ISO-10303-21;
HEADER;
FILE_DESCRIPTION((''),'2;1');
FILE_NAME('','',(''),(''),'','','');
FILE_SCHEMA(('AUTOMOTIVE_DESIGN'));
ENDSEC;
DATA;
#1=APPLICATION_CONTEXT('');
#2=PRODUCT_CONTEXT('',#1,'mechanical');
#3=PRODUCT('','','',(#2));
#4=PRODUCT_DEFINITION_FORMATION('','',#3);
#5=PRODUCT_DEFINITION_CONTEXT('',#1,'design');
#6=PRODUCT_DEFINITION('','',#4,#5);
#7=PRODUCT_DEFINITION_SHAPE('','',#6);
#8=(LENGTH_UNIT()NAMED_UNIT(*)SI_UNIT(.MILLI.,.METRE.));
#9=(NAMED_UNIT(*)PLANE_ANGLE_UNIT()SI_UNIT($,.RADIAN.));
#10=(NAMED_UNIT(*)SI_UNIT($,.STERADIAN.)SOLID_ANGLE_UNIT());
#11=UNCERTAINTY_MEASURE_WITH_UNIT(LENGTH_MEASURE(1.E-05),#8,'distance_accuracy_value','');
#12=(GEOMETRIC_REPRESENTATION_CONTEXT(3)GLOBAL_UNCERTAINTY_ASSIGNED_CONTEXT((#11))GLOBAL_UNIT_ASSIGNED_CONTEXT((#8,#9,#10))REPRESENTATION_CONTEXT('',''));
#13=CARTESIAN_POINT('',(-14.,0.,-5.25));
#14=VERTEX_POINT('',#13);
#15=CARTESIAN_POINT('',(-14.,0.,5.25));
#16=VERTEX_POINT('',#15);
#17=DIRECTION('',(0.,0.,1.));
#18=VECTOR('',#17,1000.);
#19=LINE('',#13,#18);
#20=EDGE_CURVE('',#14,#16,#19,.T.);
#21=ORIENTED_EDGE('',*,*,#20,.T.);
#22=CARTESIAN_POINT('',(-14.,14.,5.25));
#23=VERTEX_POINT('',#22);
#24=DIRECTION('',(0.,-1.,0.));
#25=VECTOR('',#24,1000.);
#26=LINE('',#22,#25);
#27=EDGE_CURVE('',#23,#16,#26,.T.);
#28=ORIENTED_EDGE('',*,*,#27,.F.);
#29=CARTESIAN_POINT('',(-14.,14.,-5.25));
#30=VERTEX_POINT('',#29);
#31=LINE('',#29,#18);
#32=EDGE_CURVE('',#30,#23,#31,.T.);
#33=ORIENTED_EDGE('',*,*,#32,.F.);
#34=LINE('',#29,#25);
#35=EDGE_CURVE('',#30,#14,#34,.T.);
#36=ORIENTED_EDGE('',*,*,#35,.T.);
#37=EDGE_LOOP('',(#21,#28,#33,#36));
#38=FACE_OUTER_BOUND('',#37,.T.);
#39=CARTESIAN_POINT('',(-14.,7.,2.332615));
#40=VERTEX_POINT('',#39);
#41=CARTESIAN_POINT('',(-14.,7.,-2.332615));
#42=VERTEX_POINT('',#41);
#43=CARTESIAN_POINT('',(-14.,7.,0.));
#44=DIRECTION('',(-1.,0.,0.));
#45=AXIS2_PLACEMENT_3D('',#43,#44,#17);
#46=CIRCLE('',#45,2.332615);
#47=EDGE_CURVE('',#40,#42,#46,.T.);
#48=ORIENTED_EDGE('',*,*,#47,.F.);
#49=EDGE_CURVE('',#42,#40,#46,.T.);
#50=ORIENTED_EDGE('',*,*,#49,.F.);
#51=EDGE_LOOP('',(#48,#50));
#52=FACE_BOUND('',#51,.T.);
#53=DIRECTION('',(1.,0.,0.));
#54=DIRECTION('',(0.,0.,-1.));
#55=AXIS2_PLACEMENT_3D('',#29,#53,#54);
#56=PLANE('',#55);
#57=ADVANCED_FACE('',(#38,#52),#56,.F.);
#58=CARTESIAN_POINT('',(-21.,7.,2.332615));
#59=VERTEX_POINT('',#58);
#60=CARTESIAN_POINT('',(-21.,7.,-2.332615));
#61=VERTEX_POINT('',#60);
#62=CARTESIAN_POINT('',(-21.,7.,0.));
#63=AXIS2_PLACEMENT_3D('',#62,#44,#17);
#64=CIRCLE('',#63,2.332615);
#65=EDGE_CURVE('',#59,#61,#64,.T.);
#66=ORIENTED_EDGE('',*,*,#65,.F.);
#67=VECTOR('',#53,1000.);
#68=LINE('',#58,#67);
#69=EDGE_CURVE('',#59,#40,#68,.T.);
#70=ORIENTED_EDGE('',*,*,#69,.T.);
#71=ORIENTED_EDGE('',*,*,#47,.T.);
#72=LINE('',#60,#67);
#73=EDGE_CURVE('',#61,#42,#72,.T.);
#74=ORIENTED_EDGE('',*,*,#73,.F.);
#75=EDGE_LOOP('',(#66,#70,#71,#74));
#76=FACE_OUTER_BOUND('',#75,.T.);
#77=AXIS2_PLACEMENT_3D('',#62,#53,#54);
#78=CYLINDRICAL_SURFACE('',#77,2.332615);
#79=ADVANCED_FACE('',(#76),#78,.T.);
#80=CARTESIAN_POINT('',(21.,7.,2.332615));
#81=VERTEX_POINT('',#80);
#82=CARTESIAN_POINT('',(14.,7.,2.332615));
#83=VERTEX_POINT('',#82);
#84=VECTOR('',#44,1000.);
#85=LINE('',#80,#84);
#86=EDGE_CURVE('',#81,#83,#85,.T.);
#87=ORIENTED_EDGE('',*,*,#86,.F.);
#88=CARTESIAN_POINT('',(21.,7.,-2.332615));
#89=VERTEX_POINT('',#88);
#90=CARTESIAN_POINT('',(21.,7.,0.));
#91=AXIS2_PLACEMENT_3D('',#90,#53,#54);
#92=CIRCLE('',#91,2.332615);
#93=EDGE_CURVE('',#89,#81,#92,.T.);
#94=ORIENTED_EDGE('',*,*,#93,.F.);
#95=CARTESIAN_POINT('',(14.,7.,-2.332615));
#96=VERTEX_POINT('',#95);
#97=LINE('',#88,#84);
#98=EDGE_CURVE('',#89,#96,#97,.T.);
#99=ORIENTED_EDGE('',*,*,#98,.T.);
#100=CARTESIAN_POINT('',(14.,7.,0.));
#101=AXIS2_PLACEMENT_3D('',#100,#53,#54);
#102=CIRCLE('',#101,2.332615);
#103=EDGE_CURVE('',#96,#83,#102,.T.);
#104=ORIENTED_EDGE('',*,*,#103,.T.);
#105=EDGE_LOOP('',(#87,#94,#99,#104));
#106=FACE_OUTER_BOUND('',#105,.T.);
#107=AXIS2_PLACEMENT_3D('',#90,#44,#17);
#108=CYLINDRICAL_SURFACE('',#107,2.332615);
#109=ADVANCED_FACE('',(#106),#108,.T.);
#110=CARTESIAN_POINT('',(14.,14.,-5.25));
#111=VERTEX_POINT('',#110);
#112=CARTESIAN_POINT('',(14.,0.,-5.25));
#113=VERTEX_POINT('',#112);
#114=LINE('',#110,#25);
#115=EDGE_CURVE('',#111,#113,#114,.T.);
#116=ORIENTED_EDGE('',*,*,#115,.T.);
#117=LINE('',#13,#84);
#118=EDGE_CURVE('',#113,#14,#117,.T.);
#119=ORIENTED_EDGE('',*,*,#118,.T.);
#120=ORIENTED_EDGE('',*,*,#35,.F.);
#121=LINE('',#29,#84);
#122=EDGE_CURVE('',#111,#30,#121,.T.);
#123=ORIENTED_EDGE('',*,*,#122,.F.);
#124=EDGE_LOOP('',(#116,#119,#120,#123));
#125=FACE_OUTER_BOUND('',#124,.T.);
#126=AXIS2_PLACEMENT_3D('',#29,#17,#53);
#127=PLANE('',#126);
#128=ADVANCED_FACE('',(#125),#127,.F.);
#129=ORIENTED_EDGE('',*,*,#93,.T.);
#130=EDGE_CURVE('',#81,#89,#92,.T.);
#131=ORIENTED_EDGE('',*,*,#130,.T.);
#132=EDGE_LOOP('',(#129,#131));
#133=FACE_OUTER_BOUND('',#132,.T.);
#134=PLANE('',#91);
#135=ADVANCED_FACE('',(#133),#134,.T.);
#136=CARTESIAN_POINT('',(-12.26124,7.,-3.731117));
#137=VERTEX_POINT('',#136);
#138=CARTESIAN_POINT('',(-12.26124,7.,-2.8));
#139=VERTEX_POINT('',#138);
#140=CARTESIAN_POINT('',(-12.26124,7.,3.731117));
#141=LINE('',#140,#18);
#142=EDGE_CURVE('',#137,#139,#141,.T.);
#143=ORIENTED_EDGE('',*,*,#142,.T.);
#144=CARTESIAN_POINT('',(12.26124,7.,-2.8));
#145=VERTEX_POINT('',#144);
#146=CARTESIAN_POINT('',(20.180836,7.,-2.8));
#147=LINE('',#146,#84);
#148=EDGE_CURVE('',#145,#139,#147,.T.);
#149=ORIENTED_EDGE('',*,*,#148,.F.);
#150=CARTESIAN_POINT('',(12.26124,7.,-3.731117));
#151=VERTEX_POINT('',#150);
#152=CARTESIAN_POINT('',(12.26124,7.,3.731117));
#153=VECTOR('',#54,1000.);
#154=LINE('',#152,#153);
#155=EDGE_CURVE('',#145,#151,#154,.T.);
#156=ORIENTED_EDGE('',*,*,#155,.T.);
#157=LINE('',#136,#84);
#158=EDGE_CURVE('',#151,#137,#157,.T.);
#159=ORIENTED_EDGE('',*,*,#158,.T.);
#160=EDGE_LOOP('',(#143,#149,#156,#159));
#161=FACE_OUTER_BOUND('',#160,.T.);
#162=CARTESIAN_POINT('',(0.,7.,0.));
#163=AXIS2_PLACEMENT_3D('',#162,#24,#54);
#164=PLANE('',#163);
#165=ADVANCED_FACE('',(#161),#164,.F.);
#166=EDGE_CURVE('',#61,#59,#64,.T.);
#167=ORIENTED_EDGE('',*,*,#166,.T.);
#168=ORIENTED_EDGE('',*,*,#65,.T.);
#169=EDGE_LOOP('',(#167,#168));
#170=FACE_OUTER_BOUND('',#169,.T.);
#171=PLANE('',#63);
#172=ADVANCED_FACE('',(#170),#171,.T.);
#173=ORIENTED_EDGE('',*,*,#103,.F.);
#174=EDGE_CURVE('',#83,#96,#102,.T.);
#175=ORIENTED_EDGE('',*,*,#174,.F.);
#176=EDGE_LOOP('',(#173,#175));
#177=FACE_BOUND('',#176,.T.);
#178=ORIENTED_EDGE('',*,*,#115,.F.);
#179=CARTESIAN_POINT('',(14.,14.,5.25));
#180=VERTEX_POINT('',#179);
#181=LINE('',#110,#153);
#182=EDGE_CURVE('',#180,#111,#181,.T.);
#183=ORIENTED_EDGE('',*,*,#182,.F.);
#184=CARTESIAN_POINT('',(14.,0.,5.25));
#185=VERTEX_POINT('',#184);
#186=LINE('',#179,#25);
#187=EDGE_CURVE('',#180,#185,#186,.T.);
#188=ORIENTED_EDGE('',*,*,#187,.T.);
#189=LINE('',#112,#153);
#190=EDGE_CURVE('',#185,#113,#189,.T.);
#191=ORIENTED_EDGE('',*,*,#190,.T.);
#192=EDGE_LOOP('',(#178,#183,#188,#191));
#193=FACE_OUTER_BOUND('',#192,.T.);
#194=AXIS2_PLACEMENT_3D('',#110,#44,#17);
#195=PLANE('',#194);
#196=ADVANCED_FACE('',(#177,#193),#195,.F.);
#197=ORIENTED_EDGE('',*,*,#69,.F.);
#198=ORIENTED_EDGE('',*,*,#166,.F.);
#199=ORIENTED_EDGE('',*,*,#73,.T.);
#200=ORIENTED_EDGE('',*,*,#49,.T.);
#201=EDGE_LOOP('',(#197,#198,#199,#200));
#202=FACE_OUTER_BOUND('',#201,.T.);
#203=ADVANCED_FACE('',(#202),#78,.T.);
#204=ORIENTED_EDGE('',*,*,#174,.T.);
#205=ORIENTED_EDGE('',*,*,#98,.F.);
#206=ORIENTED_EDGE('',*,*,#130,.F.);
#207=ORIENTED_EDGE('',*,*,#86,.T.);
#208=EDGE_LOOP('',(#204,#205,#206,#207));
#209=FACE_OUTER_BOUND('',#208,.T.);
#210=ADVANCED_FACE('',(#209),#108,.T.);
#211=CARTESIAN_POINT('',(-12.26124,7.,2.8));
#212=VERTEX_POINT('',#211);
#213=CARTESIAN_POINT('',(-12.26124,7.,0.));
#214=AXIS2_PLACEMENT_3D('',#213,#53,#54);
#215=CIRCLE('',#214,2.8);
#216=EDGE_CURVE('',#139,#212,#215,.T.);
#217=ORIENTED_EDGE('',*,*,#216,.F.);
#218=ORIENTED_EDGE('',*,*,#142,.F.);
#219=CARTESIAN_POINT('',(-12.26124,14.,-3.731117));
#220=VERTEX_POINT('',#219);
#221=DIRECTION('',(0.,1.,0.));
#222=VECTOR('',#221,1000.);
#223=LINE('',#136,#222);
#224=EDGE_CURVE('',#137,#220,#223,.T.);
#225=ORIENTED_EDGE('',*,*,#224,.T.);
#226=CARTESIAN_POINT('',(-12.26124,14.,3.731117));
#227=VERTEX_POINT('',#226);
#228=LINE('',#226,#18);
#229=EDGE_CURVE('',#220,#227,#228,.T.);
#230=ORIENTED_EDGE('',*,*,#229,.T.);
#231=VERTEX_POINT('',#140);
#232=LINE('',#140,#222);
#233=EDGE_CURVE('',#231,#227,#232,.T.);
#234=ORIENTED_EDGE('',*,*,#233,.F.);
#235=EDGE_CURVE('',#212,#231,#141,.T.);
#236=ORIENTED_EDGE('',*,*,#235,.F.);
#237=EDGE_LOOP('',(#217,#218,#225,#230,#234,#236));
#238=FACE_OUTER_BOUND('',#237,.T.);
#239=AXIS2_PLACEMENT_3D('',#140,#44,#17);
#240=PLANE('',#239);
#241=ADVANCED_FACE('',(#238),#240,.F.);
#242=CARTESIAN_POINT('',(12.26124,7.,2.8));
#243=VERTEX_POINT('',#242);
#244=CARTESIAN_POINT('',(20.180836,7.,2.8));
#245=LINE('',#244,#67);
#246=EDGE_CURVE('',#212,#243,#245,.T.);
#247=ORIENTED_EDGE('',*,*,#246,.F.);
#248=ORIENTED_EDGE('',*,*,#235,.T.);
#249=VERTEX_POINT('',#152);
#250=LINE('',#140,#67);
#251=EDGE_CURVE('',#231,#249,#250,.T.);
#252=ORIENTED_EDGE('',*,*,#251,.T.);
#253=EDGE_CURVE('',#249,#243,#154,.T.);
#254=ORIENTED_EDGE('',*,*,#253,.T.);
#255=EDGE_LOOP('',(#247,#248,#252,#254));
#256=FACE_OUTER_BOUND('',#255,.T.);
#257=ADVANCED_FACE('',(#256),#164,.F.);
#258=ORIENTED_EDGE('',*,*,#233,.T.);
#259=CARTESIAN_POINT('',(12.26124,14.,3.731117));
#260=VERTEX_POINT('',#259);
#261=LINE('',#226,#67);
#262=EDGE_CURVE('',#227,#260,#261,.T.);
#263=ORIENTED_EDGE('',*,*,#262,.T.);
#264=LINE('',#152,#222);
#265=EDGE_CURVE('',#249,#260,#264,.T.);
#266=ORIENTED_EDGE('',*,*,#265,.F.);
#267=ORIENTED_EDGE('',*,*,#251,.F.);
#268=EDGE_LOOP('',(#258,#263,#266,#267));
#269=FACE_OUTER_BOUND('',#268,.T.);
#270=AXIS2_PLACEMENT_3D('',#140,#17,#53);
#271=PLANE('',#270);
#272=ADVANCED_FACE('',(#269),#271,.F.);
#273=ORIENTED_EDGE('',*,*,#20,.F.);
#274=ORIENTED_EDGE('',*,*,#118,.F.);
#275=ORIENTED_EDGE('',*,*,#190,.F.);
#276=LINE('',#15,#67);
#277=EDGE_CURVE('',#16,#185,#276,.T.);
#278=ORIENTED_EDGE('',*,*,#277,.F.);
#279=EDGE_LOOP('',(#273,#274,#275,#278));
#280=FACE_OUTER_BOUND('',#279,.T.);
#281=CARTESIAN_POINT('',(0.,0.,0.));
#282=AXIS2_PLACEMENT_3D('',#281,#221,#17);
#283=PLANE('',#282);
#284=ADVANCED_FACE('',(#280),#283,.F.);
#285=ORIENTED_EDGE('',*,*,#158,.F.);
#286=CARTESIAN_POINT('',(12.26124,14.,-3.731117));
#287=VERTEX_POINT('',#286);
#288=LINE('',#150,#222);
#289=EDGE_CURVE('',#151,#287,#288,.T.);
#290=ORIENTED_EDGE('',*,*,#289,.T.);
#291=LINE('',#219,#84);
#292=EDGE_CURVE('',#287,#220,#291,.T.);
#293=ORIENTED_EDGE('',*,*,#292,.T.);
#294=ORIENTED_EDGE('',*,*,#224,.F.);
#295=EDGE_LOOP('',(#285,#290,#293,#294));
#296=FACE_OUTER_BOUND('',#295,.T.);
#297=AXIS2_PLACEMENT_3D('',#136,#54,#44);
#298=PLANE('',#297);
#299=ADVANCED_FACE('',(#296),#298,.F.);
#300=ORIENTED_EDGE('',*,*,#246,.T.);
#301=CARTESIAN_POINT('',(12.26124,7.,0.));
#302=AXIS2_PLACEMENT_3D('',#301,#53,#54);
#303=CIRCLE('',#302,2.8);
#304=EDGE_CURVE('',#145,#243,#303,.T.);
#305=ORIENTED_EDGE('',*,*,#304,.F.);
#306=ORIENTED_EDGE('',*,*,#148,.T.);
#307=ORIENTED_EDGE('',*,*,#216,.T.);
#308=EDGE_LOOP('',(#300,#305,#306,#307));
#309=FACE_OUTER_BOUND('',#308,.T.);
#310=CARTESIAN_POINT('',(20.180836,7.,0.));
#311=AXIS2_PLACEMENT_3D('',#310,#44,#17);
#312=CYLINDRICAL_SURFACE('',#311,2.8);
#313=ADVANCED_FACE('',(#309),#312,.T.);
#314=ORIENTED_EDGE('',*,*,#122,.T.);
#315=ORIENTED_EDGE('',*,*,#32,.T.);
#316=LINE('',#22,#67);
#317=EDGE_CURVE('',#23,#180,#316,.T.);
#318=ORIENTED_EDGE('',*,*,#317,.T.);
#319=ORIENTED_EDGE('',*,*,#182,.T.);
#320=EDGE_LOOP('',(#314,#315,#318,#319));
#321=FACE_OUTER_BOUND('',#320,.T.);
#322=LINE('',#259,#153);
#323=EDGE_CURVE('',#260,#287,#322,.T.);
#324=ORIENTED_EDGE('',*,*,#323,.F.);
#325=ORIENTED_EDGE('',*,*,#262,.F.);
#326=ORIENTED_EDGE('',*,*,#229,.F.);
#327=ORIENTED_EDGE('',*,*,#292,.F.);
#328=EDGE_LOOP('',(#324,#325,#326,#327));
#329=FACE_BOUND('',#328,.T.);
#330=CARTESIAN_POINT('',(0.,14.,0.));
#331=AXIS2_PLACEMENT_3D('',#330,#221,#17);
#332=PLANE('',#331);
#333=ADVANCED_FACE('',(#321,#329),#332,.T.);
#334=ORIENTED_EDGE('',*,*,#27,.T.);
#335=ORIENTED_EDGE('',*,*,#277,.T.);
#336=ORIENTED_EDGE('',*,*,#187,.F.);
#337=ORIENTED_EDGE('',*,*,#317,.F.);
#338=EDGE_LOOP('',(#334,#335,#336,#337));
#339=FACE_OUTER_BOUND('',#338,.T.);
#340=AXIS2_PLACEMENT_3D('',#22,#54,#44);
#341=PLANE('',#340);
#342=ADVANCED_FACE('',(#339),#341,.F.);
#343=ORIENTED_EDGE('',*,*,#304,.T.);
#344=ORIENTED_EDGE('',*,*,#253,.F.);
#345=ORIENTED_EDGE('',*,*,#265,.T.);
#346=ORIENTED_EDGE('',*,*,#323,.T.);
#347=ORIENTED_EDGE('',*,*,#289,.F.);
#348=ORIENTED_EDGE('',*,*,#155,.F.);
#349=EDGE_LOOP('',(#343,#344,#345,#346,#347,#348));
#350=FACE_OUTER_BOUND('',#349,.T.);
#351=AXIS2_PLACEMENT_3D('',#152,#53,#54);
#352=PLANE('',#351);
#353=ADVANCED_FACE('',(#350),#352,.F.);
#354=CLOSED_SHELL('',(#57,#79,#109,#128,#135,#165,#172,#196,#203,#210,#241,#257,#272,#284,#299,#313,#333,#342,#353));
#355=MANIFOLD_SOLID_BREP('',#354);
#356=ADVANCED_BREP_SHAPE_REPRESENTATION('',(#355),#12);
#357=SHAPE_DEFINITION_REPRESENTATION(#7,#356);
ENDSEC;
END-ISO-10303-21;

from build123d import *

# Parameters (mm, degrees)
SKETCH1_W           = 40
SKETCH1_H           = 15
BOSS_EXTRUDE1_DEPTH = 20
SKETCH2_W           = 35.032113562
SKETCH2_H           = 10.660333008
CUT_EXTRUDE1_DEPTH  = 10
SKETCH3_R           = 4
BOSS_EXTRUDE2_DEPTH = 35.032113562
SKETCH4_R           = 3.332307017
BOSS_EXTRUDE3_DEPTH = 10
BOSS_EXTRUDE4_START = 10
SKETCH5_R           = 3.332307017
BOSS_EXTRUDE4_DEPTH = 10
SCALE_1_SCALE       = 0.7


with BuildPart() as part:
    # Sketch1 → Boss-Extrude1 (new body)
    with BuildSketch(Plane(origin=(0, 0, 0), x_dir=(1, 0, 0), z_dir=(0, 1, 0))):
        Rectangle(SKETCH1_W, SKETCH1_H)
    extrude(amount=BOSS_EXTRUDE1_DEPTH)

    # Sketch2 → Cut-Extrude1 (cut)
    with BuildSketch(Plane(origin=(0, 20, 0), x_dir=(1, 0, 0), z_dir=(0, 1, 0))):
        Rectangle(SKETCH2_W, SKETCH2_H)
    extrude(amount=-CUT_EXTRUDE1_DEPTH, mode=Mode.SUBTRACT)

    # Sketch3 → Boss-Extrude2 (add)
    with BuildSketch(Plane(origin=(-17.516056781, 0, 0), x_dir=(0, 0, -1), z_dir=(1, 0, 0))):
        with Locations((0, 10)):
            Circle(SKETCH3_R)
    extrude(amount=BOSS_EXTRUDE2_DEPTH)

    # Sketch4 → Boss-Extrude3 (add)
    with BuildSketch(Plane.ZY.offset(20)):
        with Locations((0, 10)):
            Circle(SKETCH4_R)
    extrude(amount=BOSS_EXTRUDE3_DEPTH)

    # Sketch5 → Boss-Extrude4 (add)
    with BuildSketch(Plane(origin=(20, 0, 0), x_dir=(0, 0, -1), z_dir=(1, 0, 0)).offset(BOSS_EXTRUDE4_START)):
        with Locations(Location((0, 10, 0), (0, 0, 180))):
            Circle(SKETCH5_R)
    extrude(amount=-BOSS_EXTRUDE4_DEPTH)


with BuildPart() as part_1:
    # Scale 1: scaled about (0, 0, 0)
    add(part.part.scale(SCALE_1_SCALE))


solid = part_1.part
